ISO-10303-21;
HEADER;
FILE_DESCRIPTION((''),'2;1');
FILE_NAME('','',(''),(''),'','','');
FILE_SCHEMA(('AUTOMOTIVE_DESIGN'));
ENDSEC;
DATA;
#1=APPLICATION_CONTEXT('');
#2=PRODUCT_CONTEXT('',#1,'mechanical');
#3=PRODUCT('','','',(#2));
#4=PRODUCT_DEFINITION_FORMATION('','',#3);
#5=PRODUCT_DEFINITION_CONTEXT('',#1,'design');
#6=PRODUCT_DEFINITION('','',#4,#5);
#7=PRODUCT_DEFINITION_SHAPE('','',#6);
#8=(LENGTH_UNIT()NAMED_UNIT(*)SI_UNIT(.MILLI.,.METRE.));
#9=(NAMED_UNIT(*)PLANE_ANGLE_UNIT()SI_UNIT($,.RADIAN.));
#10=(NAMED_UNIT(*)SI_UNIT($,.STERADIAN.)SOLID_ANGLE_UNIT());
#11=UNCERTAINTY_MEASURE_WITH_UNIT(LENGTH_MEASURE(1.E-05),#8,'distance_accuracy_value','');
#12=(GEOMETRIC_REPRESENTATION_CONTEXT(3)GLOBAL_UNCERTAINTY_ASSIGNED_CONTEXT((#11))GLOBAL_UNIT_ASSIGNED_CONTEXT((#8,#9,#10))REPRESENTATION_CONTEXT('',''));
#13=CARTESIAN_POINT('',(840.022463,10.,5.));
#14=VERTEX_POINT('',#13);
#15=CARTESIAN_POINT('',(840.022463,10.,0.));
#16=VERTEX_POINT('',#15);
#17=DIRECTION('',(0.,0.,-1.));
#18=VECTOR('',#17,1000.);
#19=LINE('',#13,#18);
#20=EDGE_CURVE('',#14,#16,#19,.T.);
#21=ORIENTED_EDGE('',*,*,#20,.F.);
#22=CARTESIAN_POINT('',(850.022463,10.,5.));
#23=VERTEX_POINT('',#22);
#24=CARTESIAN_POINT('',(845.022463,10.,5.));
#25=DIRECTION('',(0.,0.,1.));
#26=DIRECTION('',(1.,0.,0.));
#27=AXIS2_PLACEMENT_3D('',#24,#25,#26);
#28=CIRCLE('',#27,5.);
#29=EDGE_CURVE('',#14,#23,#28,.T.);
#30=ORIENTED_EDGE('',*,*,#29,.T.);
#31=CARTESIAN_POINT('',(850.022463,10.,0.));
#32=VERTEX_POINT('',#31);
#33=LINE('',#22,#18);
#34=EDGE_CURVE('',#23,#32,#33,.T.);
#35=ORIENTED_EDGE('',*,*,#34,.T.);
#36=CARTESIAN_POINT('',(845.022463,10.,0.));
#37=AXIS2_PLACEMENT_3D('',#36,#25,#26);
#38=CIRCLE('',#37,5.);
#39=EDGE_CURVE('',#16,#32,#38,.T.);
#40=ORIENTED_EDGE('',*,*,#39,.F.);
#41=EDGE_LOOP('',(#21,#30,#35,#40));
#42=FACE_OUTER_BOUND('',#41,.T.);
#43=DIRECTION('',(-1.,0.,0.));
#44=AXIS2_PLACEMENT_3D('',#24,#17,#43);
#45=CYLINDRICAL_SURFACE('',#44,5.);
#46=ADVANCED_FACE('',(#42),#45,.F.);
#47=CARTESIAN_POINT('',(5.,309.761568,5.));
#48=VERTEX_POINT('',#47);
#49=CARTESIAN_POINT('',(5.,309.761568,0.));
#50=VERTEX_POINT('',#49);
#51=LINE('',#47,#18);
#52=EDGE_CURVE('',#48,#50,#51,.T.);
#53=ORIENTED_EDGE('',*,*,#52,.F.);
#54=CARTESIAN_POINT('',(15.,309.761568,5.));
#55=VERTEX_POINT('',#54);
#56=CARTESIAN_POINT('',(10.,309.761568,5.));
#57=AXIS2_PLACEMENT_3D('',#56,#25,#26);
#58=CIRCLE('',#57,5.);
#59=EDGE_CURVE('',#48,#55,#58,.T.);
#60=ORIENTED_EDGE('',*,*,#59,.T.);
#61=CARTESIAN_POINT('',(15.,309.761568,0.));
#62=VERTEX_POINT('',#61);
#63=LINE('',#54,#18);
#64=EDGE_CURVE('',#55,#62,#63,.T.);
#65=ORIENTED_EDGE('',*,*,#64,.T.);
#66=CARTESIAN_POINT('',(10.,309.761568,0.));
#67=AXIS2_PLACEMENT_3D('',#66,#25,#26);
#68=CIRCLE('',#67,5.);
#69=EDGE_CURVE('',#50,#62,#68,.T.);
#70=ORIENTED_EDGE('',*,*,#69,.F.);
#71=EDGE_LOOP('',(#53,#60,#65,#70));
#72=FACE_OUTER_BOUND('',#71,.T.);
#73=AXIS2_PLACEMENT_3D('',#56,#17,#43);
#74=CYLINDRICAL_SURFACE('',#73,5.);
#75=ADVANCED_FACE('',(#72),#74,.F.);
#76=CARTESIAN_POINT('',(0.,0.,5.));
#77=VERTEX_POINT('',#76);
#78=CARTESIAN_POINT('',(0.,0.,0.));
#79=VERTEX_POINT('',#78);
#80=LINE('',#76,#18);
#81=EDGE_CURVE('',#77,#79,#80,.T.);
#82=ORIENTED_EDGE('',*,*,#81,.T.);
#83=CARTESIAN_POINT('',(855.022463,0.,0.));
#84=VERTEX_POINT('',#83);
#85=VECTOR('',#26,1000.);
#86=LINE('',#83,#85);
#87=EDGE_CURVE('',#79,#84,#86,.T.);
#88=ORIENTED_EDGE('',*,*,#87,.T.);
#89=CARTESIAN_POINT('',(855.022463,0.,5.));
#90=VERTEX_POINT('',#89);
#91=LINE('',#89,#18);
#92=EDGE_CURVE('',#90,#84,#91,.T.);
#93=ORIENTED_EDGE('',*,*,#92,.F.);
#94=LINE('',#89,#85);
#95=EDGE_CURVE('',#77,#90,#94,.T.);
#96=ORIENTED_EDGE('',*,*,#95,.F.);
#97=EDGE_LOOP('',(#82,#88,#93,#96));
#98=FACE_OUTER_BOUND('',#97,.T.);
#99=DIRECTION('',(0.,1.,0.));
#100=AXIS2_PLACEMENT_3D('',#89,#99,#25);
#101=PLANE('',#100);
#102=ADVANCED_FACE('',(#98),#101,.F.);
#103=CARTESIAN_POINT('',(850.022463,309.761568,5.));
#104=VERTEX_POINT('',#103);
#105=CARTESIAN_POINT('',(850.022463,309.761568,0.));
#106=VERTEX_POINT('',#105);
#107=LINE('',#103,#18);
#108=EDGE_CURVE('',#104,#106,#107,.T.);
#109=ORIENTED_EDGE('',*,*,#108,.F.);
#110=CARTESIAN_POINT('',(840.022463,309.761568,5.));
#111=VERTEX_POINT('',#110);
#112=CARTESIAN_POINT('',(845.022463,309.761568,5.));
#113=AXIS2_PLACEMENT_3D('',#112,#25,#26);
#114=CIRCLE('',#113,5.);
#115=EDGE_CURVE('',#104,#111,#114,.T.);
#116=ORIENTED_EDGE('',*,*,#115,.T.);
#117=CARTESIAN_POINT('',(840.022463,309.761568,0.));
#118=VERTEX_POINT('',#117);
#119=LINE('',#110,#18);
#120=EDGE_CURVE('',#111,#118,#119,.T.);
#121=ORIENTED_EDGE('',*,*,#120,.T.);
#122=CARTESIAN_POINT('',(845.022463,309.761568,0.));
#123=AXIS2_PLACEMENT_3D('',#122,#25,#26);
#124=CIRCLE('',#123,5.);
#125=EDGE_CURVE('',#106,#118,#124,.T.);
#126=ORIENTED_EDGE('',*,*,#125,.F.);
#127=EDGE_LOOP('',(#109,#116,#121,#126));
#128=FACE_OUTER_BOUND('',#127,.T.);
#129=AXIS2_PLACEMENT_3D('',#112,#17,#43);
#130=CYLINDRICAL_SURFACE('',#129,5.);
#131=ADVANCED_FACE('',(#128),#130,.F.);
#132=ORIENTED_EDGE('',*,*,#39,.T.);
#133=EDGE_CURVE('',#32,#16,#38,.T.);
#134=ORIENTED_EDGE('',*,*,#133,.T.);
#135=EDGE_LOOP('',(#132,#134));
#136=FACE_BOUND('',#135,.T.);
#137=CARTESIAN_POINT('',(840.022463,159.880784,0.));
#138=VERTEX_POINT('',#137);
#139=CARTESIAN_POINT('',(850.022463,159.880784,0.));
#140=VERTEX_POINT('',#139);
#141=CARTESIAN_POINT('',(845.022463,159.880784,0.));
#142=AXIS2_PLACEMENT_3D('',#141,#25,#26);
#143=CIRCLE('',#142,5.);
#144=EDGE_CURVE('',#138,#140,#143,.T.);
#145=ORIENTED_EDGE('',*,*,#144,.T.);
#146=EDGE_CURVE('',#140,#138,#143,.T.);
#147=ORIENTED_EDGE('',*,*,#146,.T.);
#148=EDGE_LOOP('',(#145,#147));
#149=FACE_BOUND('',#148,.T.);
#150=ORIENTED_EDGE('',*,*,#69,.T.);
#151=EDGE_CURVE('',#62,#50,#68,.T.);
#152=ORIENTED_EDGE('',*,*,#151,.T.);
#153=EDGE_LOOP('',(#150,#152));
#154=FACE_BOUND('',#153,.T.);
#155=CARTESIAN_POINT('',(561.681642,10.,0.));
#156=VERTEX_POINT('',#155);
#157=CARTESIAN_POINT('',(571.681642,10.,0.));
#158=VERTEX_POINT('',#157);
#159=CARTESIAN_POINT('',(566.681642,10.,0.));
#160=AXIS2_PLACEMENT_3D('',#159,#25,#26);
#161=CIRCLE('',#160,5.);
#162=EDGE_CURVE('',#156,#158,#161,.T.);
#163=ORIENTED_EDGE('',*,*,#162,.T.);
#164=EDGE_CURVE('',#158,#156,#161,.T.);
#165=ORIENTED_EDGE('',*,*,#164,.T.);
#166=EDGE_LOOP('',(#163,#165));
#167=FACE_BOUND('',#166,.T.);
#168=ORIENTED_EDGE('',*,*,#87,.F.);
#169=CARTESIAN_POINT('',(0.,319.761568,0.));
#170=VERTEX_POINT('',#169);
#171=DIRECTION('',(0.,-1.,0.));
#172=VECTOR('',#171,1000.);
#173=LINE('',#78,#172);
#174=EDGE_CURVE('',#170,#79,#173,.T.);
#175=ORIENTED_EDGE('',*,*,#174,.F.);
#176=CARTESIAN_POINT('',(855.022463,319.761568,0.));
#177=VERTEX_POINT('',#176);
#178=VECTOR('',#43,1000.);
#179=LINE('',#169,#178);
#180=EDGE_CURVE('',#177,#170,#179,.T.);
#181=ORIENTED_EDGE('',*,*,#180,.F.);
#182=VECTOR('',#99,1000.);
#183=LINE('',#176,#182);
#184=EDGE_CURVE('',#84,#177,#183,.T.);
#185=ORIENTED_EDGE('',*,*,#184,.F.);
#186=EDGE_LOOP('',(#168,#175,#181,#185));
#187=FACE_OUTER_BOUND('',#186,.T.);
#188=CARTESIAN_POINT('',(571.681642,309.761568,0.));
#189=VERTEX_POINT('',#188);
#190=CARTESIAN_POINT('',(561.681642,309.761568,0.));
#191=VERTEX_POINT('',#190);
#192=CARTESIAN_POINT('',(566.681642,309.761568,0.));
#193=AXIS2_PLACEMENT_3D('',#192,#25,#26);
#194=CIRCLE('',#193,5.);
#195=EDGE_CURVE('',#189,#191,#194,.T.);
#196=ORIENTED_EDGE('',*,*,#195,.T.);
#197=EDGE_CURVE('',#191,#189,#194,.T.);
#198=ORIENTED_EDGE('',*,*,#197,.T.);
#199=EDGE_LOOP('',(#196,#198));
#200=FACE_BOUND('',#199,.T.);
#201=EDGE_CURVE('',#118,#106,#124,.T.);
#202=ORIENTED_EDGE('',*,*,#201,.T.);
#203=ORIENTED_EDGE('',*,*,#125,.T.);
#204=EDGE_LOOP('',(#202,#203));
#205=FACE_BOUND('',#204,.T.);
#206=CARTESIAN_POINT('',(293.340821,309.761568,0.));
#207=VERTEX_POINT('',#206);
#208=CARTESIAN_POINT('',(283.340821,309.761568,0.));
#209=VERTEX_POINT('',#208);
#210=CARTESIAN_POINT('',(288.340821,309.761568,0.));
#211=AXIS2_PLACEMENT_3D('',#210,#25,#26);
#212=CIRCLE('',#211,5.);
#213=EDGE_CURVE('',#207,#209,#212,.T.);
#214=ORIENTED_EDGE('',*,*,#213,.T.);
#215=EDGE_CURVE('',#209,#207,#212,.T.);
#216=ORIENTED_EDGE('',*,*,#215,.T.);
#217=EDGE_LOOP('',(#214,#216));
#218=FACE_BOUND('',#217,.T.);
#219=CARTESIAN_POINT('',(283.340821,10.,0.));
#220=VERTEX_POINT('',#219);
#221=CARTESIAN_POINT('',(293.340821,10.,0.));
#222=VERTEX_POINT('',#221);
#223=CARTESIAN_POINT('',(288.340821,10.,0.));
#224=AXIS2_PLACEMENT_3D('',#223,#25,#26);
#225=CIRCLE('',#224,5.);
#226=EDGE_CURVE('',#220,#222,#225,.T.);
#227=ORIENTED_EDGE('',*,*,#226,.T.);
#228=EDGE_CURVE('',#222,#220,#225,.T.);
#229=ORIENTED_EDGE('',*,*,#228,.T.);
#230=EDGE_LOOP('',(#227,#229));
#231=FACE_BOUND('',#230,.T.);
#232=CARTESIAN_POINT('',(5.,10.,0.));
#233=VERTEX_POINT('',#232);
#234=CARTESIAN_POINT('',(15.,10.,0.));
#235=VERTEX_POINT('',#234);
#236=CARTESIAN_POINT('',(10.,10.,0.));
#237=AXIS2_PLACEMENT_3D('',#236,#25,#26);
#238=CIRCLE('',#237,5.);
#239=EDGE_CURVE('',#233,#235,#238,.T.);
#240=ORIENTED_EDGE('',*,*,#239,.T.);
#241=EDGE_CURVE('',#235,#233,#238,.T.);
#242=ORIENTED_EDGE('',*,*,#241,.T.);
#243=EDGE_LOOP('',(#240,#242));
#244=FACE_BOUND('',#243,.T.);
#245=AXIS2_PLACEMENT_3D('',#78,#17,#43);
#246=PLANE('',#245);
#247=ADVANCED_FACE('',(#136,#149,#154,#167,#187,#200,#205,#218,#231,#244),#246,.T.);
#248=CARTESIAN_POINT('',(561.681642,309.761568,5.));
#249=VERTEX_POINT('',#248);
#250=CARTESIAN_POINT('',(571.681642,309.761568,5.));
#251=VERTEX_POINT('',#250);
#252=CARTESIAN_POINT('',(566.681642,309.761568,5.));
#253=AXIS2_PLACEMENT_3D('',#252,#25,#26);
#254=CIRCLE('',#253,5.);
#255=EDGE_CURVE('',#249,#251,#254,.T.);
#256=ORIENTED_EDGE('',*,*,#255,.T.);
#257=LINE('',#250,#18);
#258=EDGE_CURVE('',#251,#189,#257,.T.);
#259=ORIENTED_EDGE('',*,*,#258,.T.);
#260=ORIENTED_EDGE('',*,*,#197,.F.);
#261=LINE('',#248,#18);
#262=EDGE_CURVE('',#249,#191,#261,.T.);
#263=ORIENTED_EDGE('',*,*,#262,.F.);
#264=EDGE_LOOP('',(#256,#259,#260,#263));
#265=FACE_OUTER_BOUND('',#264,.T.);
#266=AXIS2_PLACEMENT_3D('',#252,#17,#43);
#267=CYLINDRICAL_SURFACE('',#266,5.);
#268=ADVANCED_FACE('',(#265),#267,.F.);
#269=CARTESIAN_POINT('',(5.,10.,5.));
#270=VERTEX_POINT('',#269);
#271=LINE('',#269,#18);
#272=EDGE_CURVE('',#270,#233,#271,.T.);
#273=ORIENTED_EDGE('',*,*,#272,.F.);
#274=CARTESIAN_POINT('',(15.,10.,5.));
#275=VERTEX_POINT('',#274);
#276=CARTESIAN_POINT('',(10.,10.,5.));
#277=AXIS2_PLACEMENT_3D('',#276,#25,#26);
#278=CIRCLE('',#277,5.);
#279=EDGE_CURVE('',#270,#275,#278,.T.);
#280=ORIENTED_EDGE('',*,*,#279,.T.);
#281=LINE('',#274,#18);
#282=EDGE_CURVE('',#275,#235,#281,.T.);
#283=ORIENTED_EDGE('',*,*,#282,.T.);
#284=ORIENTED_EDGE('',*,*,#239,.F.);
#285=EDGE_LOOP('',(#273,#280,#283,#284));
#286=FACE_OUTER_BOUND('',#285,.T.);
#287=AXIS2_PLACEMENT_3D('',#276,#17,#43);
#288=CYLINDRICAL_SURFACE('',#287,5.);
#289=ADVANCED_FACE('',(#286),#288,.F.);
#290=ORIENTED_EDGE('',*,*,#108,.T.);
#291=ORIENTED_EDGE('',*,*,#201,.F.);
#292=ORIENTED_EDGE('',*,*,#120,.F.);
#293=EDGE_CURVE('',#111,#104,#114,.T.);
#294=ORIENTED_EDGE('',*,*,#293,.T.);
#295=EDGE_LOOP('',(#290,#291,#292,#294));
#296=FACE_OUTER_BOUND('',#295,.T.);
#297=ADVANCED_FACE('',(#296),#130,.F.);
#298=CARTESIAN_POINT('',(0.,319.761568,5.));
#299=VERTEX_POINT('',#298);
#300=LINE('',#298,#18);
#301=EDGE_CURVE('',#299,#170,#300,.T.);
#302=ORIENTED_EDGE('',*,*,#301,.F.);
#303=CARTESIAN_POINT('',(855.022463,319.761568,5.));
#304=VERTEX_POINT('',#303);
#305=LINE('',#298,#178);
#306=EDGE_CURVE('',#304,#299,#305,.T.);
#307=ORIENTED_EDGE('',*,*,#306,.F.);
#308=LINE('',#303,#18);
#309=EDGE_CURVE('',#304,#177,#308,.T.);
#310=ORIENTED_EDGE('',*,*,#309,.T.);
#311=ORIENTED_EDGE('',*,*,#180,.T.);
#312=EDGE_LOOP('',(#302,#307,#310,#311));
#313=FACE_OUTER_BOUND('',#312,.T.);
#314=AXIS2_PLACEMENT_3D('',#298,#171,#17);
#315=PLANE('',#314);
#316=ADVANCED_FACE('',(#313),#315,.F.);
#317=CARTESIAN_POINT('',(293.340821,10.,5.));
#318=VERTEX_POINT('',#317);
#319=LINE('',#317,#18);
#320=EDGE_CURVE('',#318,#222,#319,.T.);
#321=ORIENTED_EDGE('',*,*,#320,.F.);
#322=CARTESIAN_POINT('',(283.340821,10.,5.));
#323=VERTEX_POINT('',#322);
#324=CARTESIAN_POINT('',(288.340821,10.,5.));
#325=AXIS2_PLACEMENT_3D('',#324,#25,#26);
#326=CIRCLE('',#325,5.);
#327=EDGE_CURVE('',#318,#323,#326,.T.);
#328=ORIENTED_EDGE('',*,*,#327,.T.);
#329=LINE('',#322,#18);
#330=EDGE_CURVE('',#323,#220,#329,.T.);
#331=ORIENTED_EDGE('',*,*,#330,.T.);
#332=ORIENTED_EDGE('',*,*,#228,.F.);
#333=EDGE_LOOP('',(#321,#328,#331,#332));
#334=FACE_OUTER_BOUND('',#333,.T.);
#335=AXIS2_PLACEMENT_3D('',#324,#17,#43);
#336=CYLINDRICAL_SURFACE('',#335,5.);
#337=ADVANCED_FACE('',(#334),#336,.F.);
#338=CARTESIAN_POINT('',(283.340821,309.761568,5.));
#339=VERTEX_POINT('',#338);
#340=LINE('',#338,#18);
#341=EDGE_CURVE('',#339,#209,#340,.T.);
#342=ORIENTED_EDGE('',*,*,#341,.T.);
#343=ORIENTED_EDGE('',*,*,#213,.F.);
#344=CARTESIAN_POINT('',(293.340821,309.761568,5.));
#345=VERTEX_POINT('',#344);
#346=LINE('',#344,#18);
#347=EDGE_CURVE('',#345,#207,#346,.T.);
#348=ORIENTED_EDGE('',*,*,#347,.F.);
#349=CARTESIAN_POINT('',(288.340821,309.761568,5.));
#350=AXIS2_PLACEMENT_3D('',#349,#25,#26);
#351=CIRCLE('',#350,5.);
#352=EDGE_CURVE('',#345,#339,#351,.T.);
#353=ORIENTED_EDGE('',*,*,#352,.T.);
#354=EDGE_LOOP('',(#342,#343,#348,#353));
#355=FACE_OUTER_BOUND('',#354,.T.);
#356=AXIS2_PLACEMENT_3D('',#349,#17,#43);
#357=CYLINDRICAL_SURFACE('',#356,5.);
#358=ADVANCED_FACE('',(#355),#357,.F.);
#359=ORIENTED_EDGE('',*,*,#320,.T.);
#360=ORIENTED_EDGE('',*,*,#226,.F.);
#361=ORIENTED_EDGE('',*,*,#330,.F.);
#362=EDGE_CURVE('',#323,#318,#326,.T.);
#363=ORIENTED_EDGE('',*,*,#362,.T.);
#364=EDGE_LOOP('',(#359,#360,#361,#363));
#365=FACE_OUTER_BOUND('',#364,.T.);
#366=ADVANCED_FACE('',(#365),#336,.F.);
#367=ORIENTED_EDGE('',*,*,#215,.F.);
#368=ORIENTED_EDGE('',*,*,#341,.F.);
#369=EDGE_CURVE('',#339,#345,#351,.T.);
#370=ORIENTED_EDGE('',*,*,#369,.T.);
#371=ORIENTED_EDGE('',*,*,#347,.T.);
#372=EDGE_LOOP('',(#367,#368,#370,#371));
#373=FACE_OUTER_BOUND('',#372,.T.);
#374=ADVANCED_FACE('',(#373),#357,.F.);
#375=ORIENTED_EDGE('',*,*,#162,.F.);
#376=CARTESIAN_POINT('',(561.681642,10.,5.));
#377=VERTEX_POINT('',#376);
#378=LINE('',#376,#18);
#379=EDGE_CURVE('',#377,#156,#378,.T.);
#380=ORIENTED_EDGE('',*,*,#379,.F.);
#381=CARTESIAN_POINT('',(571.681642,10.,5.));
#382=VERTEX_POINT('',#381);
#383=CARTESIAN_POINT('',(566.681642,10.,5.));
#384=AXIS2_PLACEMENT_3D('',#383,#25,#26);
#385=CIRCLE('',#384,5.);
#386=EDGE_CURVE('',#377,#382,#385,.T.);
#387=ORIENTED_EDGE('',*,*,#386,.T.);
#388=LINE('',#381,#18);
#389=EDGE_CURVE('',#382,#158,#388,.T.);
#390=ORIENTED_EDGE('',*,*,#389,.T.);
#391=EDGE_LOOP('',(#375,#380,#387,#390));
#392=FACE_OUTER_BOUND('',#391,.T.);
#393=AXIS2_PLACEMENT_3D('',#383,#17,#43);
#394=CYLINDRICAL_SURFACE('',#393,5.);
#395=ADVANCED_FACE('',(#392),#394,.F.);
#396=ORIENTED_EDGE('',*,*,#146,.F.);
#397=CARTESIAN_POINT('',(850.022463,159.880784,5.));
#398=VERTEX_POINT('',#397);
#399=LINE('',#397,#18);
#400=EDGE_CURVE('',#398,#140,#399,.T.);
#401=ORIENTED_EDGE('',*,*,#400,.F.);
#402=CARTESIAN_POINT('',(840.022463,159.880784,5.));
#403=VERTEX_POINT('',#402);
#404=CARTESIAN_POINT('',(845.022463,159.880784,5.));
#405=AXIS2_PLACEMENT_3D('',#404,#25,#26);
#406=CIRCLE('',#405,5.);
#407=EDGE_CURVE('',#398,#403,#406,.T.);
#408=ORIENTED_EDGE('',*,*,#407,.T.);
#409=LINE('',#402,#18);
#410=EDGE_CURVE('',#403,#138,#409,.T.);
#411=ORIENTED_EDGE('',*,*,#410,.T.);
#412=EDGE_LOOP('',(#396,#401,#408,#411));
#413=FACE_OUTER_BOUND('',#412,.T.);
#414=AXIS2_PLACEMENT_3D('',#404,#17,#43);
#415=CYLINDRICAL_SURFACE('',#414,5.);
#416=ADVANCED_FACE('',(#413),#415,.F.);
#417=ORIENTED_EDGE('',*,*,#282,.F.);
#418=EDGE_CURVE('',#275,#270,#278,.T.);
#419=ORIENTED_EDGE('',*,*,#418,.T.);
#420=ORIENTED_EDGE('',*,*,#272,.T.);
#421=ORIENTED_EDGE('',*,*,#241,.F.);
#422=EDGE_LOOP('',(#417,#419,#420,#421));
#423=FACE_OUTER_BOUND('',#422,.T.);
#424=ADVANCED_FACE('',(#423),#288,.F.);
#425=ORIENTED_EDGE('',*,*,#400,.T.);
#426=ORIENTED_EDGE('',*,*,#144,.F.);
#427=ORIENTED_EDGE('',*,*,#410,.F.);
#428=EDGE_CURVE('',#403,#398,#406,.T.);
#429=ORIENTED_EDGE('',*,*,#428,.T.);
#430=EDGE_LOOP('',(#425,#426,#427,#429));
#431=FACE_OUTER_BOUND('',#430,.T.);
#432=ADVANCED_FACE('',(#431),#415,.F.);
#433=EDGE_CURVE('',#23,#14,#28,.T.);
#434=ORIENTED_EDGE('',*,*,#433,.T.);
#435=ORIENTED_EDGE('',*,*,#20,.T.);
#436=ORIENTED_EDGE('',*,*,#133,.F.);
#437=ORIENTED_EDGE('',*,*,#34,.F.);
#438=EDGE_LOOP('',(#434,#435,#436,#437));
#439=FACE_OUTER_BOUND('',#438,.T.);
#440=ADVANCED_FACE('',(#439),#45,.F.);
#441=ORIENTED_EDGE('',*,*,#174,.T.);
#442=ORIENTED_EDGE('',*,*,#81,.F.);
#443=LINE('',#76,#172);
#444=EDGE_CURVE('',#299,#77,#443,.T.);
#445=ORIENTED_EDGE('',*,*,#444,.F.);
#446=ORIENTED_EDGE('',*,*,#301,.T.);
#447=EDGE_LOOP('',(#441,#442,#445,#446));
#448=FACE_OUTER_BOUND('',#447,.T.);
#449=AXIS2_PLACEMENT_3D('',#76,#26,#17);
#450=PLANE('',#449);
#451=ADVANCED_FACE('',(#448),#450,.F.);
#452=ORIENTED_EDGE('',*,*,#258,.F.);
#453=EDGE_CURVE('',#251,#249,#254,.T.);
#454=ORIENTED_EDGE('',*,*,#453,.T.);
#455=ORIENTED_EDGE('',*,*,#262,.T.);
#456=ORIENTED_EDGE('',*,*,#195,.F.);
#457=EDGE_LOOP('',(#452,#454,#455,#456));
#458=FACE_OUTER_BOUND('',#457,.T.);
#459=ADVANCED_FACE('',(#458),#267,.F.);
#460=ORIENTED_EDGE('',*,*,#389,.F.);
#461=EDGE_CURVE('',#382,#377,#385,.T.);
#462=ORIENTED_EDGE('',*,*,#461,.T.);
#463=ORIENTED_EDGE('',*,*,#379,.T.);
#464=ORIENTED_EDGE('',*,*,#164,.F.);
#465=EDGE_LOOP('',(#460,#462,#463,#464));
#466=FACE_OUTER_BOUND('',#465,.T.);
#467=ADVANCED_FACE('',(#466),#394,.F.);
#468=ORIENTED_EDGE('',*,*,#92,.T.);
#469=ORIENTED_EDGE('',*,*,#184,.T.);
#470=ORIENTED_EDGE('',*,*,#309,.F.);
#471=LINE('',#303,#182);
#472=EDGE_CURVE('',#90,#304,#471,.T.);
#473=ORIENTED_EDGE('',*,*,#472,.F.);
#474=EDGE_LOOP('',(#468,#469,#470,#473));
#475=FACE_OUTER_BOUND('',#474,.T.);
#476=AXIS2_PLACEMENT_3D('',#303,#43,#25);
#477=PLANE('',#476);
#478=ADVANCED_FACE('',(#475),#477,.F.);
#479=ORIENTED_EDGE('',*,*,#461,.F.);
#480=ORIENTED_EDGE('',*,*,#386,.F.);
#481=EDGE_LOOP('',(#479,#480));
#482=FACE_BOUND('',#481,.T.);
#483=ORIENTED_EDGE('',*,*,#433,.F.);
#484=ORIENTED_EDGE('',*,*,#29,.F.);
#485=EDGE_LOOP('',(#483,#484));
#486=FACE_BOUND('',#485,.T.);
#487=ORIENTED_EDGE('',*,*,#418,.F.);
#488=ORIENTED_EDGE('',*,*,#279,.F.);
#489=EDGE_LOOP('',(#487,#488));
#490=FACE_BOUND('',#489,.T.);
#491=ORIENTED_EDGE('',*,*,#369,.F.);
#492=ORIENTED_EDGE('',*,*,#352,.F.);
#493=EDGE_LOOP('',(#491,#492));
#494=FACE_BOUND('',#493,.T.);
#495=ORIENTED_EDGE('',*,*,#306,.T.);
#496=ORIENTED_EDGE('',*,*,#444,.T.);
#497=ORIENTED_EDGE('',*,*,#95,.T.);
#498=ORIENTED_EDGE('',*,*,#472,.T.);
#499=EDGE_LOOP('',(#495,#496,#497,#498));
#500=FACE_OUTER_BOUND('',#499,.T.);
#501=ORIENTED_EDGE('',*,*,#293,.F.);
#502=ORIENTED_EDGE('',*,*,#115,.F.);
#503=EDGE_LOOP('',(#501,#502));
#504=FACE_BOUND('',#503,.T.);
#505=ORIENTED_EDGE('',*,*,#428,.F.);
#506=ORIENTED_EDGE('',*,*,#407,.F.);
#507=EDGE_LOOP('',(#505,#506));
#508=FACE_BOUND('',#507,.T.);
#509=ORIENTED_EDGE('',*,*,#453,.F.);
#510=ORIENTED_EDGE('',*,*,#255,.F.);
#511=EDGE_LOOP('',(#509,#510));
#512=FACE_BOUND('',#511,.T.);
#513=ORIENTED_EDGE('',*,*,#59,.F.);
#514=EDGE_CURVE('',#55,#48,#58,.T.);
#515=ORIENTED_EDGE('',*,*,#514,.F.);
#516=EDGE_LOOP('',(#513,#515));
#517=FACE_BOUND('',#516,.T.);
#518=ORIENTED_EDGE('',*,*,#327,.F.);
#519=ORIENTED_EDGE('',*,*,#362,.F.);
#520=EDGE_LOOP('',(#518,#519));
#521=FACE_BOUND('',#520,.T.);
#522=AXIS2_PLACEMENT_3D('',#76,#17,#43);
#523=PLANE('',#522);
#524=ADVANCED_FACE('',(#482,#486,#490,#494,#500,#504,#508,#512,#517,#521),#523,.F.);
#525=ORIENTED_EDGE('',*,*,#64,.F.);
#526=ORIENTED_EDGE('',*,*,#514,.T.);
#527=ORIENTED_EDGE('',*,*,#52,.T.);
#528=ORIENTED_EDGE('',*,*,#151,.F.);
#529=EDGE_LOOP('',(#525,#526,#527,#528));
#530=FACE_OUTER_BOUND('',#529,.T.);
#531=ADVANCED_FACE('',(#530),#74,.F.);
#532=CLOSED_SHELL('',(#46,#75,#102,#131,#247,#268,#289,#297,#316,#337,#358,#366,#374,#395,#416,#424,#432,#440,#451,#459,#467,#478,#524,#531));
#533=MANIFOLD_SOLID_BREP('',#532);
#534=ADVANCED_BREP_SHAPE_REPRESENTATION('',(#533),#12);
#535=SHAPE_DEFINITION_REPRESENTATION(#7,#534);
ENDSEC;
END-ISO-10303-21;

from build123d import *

# Parameters (mm, degrees)
SKETCH1_W           = 855.022462921
SKETCH1_H           = 319.761568038
SKETCH1_R           = 5
BOSS_EXTRUDE1_DEPTH = 5


with BuildPart() as part:
    # Sketch1 → Boss-Extrude1 (new body)
    with BuildSketch(Plane.XY):
        with Locations((427.511231461, 159.880784019)):
            Rectangle(SKETCH1_W, SKETCH1_H)
        with Locations((10, 309.761568038)):
            Circle(SKETCH1_R, mode=Mode.SUBTRACT)
        with Locations((845.022462921, 309.761568038)):
            Circle(SKETCH1_R, mode=Mode.SUBTRACT)
        with Locations((10, 10)):
            Circle(SKETCH1_R, mode=Mode.SUBTRACT)
        with Locations((845.022462921, 10)):
            Circle(SKETCH1_R, mode=Mode.SUBTRACT)
        with Locations((288.340820974, 309.761568038)):
            Circle(SKETCH1_R, mode=Mode.SUBTRACT)
        with Locations((288.340820974, 10)):
            Circle(SKETCH1_R, mode=Mode.SUBTRACT)
        with Locations((566.681641947, 309.761568038)):
            Circle(SKETCH1_R, mode=Mode.SUBTRACT)
        with Locations((566.681641947, 10)):
            Circle(SKETCH1_R, mode=Mode.SUBTRACT)
        with Locations((845.022462921, 159.880784019)):
            Circle(SKETCH1_R, mode=Mode.SUBTRACT)
    extrude(amount=BOSS_EXTRUDE1_DEPTH)


solid = part.part
